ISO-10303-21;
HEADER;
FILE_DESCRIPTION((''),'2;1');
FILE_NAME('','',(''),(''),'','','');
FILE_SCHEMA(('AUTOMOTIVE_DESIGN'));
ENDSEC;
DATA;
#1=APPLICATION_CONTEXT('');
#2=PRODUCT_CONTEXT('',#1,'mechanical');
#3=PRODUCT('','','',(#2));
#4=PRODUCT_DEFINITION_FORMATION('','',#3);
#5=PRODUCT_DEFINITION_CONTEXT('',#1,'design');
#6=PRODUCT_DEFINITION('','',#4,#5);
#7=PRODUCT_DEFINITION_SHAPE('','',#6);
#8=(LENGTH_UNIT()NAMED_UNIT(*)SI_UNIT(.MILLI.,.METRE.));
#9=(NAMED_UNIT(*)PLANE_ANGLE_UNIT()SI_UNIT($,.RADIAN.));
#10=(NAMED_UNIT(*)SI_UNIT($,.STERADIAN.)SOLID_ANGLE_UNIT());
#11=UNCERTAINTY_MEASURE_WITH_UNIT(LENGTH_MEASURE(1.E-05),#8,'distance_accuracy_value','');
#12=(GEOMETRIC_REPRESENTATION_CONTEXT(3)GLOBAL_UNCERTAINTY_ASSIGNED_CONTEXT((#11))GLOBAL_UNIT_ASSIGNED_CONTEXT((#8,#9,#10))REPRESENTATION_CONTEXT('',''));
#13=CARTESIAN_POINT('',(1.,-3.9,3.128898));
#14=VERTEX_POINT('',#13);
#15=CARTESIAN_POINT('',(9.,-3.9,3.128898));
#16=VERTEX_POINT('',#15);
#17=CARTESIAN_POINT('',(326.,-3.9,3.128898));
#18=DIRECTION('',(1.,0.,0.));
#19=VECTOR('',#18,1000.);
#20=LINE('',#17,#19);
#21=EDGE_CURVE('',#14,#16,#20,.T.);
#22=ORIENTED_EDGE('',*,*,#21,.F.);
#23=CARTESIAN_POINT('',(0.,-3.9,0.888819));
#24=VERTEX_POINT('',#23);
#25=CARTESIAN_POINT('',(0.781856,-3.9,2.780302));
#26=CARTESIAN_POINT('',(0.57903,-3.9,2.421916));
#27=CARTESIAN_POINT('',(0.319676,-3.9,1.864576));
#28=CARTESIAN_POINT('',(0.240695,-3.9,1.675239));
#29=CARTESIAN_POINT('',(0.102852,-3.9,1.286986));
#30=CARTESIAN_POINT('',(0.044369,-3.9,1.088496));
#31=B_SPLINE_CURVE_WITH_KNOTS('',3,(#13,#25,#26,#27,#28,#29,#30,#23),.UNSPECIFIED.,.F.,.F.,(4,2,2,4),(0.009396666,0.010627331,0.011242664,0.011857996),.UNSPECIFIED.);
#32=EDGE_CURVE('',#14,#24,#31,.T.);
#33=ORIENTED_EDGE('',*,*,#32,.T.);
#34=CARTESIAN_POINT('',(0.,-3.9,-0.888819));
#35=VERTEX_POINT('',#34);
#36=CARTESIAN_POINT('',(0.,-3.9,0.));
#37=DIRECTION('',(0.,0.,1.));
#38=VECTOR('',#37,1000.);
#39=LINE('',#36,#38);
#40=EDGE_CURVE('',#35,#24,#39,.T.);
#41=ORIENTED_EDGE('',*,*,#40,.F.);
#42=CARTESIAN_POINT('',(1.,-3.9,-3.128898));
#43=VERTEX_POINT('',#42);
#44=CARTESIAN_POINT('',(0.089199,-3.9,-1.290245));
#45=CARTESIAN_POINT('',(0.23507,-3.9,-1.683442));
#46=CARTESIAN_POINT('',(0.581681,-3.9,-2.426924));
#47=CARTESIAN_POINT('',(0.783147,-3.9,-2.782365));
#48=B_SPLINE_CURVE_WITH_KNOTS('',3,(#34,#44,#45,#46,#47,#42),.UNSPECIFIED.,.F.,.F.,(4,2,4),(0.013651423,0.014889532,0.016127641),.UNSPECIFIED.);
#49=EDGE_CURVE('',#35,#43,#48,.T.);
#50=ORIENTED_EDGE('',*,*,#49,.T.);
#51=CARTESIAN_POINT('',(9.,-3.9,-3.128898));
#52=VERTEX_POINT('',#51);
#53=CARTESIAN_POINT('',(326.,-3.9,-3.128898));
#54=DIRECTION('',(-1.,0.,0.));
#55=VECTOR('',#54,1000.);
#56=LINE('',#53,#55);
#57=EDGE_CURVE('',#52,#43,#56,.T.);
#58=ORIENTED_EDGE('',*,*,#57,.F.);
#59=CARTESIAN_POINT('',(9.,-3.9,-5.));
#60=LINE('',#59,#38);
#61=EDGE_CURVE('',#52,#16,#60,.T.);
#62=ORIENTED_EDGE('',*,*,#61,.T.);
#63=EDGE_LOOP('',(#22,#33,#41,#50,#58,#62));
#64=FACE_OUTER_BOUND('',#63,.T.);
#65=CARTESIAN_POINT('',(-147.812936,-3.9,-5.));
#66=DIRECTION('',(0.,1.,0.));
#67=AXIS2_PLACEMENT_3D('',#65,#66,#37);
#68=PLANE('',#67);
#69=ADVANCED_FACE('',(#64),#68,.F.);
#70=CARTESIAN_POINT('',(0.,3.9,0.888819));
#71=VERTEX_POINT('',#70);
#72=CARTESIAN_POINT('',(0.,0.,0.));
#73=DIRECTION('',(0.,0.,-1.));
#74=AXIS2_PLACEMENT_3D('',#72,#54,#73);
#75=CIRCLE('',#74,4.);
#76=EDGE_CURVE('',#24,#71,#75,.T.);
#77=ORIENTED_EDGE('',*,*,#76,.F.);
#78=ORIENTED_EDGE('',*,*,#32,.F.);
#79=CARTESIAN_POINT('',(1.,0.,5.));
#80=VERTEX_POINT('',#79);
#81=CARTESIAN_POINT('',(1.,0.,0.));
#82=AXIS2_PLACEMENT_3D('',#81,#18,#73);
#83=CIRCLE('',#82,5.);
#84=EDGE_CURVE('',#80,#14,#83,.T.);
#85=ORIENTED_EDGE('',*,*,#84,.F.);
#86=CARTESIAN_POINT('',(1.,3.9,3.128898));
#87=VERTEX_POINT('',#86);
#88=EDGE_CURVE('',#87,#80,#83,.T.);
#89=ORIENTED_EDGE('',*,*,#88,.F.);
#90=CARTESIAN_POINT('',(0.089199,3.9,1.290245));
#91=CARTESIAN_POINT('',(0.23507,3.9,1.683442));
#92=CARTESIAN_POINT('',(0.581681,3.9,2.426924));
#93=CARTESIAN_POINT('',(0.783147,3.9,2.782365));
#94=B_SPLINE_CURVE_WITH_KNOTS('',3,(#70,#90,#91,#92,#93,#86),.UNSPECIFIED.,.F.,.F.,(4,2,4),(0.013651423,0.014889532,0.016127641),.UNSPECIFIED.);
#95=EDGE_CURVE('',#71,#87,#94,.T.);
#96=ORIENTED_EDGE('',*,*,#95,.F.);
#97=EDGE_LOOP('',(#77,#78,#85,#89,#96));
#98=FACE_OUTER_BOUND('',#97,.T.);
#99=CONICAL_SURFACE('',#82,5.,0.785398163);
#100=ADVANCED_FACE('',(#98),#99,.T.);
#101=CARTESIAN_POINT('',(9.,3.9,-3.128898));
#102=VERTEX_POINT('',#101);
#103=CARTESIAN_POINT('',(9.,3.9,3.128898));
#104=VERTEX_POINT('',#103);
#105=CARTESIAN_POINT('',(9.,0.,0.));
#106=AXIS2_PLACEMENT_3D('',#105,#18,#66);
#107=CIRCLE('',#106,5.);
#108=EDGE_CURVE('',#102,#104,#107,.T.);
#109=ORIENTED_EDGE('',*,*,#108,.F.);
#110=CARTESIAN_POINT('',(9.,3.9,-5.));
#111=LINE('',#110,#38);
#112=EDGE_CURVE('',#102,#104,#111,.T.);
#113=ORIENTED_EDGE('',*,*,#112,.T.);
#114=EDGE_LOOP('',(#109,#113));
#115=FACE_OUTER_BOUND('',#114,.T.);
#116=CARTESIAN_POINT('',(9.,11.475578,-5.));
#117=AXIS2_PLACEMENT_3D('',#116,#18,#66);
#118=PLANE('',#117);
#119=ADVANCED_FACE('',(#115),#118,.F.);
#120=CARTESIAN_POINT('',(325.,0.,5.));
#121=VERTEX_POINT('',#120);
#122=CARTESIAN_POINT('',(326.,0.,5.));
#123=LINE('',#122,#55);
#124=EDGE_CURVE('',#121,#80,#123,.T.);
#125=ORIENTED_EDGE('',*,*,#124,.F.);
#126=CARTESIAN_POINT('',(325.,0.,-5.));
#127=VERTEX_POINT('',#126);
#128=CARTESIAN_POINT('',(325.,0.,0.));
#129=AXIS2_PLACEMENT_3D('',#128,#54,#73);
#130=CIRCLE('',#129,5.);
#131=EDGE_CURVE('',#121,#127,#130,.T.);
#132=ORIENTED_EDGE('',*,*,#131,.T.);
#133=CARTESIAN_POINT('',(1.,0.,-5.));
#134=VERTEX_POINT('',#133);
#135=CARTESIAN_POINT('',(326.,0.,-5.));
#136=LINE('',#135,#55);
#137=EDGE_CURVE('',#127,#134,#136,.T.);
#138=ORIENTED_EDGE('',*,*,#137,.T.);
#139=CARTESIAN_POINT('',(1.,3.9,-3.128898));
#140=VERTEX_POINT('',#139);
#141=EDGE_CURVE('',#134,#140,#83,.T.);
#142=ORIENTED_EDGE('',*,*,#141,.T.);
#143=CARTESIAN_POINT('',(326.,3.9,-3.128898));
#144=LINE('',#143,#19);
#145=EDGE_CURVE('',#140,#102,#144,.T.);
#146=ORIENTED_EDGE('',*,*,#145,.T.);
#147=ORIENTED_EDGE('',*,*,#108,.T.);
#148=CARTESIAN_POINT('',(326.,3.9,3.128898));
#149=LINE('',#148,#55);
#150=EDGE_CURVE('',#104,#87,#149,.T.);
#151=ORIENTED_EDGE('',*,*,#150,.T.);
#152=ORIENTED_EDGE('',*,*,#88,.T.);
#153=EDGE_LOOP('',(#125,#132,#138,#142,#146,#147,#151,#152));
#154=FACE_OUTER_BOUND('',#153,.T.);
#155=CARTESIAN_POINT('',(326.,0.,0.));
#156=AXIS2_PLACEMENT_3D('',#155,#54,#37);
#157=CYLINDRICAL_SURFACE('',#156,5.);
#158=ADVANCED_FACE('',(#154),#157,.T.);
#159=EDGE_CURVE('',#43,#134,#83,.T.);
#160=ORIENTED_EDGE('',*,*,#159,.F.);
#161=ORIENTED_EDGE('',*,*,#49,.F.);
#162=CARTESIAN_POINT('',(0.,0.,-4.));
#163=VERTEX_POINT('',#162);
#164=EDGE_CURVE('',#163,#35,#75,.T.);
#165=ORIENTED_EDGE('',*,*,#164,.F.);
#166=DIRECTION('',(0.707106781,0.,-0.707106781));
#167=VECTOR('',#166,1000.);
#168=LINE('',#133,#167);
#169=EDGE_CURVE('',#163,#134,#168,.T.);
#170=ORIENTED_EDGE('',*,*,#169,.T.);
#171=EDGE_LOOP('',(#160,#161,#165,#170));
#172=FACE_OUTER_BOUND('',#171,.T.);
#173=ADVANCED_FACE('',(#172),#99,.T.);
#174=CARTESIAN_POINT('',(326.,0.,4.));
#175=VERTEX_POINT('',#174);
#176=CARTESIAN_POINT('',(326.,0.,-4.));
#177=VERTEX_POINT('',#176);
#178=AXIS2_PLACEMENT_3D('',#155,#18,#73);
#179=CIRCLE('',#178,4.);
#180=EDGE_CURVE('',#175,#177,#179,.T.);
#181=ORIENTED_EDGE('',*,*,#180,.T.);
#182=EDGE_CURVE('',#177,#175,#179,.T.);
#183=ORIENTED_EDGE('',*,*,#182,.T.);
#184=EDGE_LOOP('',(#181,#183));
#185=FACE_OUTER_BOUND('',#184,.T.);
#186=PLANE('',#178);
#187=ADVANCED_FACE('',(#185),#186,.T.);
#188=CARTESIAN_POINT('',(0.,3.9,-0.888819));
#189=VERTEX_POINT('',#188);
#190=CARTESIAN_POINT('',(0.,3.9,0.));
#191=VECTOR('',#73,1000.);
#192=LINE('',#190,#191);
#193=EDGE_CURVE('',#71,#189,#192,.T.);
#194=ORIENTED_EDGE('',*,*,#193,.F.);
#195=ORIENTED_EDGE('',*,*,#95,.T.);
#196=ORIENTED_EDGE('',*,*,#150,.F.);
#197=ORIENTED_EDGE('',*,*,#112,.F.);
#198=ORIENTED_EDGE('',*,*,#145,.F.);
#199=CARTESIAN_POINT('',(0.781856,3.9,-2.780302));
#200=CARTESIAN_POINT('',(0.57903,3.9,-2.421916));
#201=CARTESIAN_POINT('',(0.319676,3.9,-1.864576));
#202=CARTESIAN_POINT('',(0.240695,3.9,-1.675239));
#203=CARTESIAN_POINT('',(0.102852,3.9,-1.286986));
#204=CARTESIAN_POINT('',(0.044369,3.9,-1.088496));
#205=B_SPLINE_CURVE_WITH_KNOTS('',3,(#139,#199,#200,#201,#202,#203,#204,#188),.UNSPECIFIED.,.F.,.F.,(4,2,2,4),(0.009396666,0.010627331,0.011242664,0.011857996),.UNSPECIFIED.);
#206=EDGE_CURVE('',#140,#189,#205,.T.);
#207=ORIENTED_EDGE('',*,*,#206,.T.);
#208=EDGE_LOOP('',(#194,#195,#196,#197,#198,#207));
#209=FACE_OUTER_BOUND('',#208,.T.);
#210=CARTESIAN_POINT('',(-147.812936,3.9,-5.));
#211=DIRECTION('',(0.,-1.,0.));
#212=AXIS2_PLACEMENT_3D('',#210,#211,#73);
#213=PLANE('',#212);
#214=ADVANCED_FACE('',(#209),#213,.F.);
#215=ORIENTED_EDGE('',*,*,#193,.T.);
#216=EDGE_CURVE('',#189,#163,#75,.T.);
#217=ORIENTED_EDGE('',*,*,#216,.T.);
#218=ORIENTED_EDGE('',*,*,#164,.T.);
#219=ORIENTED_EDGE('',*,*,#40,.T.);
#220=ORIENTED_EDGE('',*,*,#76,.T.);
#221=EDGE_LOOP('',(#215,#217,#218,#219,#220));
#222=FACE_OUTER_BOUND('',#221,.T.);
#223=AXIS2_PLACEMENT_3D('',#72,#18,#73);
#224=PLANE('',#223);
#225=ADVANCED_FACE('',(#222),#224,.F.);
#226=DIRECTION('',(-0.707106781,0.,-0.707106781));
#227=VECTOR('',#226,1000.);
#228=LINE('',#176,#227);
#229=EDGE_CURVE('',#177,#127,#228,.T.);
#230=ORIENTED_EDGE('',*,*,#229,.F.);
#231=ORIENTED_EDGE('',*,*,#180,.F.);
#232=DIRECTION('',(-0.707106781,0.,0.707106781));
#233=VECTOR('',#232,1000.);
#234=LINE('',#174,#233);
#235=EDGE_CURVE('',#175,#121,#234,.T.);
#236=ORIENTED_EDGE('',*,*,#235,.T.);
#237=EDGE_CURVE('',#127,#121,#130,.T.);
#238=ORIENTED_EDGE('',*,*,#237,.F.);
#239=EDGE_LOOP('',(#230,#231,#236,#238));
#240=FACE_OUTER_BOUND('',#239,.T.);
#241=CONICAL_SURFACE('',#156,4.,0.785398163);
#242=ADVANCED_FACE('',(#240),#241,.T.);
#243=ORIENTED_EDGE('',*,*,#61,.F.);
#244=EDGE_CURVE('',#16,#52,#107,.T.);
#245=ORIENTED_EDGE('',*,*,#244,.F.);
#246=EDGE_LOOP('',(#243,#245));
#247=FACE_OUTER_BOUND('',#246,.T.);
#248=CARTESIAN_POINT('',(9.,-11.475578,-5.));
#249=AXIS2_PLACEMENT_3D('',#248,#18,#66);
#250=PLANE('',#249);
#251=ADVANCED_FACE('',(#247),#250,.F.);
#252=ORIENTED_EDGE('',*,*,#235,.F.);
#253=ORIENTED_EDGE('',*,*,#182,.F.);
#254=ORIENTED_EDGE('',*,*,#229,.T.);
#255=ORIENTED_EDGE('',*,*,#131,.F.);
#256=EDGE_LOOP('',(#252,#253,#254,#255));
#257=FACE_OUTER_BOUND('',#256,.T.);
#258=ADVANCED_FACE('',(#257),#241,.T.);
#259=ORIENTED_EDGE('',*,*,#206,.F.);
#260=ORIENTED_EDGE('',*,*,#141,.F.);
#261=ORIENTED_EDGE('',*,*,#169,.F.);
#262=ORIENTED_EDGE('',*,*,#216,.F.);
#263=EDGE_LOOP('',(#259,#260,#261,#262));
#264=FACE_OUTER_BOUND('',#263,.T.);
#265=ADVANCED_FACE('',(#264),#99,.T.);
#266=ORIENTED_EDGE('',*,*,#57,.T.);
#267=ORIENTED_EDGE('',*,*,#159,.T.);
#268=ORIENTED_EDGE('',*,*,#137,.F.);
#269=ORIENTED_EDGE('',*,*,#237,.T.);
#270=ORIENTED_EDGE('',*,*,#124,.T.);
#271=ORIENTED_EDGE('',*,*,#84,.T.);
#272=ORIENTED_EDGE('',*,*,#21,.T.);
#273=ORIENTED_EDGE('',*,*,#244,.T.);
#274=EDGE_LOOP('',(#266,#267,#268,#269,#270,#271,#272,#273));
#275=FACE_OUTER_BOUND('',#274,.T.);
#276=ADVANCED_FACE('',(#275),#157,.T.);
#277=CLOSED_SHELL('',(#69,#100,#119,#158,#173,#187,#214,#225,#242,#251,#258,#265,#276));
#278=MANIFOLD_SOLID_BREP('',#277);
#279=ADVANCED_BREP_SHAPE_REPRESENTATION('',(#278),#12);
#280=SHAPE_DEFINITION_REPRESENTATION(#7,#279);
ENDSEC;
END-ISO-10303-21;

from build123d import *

# Parameters (mm, degrees)
SKETCH1_R               = 5
BOSS_EXTRUDE1_DEPTH     = 326
CHAMFER1_SIZE           = 1
CUT_EXTRUDE1_DEPTH      = 327.076678099
CUT_EXTRUDE1_DEPTH_BACK = 327.076678099
SKETCH8_W               = 156.812935598
SKETCH8_H               = 4.242810574
SKETCH8_H_2             = 7.575578147


with BuildPart() as part:
    # Sketch1 → Boss-Extrude1 (new body)
    with BuildSketch(Plane(origin=(0, 0, 0), x_dir=(0, 0, -1), z_dir=(1, 0, 0))):
        Circle(SKETCH1_R)
    extrude(amount=BOSS_EXTRUDE1_DEPTH)

    # Chamfer1
    chamfer1_edges = [part.edges().sort_by_distance(p)[0] for p in [
        (0, 0, 5),
        (326, 0, 5),
    ]]
    chamfer(chamfer1_edges, length=CHAMFER1_SIZE)

    # Sketch8 → Cut-Extrude1 (cut, two sides: drawn at the far end of the back side and taken through both)
    with BuildSketch(Plane.XY.offset(-CUT_EXTRUDE1_DEPTH_BACK)):
        with Locations((413.406467799, 6.021405287)):
            Rectangle(SKETCH8_W, SKETCH8_H)
        with Locations((413.406467799, -6.021405287)):
            Rectangle(SKETCH8_W, SKETCH8_H)
        with Locations((-69.406467799, 7.687789074)):
            Rectangle(SKETCH8_W, SKETCH8_H_2)
        with Locations((-69.406467799, -7.687789074)):
            Rectangle(SKETCH8_W, SKETCH8_H_2)
    extrude(amount=CUT_EXTRUDE1_DEPTH + CUT_EXTRUDE1_DEPTH_BACK, mode=Mode.SUBTRACT)


solid = part.part
